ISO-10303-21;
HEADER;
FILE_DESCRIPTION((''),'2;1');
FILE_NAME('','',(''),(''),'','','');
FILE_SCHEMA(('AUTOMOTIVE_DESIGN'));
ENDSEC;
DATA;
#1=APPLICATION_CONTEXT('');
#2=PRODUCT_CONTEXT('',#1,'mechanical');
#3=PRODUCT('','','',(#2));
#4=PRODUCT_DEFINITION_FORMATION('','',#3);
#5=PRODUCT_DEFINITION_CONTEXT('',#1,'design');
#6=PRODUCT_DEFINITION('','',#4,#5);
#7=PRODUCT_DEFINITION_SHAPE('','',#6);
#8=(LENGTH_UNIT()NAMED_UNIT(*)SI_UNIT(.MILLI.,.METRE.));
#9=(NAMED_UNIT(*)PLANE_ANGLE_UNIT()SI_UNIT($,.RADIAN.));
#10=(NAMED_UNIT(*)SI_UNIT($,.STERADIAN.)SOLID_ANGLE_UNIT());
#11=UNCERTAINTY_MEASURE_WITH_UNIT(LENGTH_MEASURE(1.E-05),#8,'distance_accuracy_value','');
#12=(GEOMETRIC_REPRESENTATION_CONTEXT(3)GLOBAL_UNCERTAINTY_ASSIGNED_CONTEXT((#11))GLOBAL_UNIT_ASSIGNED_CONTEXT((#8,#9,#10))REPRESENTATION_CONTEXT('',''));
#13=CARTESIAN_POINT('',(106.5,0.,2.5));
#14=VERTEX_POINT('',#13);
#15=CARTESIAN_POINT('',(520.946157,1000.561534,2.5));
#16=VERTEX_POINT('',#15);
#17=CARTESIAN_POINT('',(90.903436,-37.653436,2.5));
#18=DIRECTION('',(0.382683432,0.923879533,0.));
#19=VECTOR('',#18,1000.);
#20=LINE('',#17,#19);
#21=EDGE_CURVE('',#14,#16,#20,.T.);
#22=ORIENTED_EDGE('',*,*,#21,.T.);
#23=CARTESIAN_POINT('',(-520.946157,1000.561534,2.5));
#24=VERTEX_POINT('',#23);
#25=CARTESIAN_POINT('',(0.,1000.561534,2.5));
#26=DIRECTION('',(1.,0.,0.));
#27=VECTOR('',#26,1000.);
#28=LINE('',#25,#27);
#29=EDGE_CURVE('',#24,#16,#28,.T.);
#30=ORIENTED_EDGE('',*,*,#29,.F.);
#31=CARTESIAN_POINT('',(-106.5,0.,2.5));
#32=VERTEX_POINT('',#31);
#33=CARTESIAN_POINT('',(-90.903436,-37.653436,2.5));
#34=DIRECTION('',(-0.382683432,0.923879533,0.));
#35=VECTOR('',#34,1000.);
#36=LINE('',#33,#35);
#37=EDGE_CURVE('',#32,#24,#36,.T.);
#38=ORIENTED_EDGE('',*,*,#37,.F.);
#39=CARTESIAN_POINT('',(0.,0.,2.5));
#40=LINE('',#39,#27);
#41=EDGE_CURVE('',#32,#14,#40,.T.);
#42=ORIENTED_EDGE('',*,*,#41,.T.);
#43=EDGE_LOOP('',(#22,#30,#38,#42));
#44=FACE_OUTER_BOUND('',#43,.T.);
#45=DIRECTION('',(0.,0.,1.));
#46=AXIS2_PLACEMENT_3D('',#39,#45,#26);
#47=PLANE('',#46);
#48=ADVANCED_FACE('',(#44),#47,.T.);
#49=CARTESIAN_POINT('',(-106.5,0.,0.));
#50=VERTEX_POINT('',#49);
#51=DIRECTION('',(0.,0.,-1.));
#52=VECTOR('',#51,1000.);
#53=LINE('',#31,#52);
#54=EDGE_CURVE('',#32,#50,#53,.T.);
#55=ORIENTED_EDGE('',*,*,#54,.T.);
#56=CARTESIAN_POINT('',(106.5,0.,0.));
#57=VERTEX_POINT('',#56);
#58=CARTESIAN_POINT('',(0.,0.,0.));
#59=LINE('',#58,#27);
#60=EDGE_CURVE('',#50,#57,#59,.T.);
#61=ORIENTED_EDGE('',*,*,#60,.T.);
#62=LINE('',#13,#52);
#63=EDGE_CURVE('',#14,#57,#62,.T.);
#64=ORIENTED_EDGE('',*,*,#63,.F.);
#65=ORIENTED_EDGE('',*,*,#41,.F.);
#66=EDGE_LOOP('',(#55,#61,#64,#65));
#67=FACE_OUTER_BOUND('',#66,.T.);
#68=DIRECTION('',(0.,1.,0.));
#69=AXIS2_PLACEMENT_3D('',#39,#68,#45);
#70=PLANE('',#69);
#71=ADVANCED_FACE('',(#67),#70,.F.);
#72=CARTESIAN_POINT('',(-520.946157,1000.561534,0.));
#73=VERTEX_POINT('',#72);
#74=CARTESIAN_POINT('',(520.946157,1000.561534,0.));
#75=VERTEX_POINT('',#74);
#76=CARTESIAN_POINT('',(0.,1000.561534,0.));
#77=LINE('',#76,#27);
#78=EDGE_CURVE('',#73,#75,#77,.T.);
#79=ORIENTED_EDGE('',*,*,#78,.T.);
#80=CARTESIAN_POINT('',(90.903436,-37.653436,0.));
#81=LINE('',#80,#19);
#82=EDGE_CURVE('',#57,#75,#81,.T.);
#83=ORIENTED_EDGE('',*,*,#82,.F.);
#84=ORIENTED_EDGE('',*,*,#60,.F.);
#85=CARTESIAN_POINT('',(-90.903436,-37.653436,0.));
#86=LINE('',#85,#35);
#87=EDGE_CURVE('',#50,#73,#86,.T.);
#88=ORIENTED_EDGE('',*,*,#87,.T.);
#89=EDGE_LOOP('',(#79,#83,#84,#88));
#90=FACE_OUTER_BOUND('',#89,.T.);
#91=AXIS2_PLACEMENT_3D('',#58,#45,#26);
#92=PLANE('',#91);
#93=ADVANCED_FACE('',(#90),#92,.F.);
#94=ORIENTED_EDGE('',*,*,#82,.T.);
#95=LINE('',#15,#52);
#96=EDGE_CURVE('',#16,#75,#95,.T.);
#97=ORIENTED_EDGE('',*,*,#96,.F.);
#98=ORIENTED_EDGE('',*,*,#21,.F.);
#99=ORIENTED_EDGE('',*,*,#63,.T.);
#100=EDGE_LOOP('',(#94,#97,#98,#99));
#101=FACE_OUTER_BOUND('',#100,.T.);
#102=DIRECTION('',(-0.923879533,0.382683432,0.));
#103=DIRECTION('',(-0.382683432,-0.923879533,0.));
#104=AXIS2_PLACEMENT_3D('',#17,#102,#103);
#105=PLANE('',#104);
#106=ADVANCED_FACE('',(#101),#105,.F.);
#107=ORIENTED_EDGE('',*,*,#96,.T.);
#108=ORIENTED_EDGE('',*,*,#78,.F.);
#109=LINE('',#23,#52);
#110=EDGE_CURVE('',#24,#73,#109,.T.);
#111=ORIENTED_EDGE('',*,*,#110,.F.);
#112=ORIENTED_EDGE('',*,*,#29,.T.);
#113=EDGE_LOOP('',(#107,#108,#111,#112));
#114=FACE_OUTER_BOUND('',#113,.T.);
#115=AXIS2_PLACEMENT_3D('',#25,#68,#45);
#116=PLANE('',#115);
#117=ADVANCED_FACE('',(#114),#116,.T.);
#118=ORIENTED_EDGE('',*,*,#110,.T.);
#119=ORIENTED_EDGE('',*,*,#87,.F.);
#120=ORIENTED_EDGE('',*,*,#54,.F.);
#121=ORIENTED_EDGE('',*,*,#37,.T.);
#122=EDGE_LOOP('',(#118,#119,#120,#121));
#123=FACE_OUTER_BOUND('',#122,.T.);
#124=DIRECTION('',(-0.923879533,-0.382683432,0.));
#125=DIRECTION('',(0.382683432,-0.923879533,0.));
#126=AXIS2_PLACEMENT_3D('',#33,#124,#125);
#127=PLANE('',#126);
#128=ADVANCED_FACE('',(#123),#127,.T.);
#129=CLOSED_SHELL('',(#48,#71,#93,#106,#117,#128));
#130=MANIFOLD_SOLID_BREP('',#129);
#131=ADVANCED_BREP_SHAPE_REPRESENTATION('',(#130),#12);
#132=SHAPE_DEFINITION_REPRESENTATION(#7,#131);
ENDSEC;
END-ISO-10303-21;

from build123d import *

# Parameters (mm, degrees)
BOSS_EXTRUDE1_DEPTH = 2.5


with BuildPart() as part:
    # Sketch1 → Boss-Extrude1 (new body)
    with BuildSketch(Plane.XY):
        Polygon((0, 1000.56153371), (0, 0), (106.5, 0), (520.946157251, 1000.56153371), align=None)
        Polygon((-106.5, 0), (0, 0), (0, 1000.56153371), (-520.946157251, 1000.56153371), align=None)
    extrude(amount=BOSS_EXTRUDE1_DEPTH)


solid = part.part
